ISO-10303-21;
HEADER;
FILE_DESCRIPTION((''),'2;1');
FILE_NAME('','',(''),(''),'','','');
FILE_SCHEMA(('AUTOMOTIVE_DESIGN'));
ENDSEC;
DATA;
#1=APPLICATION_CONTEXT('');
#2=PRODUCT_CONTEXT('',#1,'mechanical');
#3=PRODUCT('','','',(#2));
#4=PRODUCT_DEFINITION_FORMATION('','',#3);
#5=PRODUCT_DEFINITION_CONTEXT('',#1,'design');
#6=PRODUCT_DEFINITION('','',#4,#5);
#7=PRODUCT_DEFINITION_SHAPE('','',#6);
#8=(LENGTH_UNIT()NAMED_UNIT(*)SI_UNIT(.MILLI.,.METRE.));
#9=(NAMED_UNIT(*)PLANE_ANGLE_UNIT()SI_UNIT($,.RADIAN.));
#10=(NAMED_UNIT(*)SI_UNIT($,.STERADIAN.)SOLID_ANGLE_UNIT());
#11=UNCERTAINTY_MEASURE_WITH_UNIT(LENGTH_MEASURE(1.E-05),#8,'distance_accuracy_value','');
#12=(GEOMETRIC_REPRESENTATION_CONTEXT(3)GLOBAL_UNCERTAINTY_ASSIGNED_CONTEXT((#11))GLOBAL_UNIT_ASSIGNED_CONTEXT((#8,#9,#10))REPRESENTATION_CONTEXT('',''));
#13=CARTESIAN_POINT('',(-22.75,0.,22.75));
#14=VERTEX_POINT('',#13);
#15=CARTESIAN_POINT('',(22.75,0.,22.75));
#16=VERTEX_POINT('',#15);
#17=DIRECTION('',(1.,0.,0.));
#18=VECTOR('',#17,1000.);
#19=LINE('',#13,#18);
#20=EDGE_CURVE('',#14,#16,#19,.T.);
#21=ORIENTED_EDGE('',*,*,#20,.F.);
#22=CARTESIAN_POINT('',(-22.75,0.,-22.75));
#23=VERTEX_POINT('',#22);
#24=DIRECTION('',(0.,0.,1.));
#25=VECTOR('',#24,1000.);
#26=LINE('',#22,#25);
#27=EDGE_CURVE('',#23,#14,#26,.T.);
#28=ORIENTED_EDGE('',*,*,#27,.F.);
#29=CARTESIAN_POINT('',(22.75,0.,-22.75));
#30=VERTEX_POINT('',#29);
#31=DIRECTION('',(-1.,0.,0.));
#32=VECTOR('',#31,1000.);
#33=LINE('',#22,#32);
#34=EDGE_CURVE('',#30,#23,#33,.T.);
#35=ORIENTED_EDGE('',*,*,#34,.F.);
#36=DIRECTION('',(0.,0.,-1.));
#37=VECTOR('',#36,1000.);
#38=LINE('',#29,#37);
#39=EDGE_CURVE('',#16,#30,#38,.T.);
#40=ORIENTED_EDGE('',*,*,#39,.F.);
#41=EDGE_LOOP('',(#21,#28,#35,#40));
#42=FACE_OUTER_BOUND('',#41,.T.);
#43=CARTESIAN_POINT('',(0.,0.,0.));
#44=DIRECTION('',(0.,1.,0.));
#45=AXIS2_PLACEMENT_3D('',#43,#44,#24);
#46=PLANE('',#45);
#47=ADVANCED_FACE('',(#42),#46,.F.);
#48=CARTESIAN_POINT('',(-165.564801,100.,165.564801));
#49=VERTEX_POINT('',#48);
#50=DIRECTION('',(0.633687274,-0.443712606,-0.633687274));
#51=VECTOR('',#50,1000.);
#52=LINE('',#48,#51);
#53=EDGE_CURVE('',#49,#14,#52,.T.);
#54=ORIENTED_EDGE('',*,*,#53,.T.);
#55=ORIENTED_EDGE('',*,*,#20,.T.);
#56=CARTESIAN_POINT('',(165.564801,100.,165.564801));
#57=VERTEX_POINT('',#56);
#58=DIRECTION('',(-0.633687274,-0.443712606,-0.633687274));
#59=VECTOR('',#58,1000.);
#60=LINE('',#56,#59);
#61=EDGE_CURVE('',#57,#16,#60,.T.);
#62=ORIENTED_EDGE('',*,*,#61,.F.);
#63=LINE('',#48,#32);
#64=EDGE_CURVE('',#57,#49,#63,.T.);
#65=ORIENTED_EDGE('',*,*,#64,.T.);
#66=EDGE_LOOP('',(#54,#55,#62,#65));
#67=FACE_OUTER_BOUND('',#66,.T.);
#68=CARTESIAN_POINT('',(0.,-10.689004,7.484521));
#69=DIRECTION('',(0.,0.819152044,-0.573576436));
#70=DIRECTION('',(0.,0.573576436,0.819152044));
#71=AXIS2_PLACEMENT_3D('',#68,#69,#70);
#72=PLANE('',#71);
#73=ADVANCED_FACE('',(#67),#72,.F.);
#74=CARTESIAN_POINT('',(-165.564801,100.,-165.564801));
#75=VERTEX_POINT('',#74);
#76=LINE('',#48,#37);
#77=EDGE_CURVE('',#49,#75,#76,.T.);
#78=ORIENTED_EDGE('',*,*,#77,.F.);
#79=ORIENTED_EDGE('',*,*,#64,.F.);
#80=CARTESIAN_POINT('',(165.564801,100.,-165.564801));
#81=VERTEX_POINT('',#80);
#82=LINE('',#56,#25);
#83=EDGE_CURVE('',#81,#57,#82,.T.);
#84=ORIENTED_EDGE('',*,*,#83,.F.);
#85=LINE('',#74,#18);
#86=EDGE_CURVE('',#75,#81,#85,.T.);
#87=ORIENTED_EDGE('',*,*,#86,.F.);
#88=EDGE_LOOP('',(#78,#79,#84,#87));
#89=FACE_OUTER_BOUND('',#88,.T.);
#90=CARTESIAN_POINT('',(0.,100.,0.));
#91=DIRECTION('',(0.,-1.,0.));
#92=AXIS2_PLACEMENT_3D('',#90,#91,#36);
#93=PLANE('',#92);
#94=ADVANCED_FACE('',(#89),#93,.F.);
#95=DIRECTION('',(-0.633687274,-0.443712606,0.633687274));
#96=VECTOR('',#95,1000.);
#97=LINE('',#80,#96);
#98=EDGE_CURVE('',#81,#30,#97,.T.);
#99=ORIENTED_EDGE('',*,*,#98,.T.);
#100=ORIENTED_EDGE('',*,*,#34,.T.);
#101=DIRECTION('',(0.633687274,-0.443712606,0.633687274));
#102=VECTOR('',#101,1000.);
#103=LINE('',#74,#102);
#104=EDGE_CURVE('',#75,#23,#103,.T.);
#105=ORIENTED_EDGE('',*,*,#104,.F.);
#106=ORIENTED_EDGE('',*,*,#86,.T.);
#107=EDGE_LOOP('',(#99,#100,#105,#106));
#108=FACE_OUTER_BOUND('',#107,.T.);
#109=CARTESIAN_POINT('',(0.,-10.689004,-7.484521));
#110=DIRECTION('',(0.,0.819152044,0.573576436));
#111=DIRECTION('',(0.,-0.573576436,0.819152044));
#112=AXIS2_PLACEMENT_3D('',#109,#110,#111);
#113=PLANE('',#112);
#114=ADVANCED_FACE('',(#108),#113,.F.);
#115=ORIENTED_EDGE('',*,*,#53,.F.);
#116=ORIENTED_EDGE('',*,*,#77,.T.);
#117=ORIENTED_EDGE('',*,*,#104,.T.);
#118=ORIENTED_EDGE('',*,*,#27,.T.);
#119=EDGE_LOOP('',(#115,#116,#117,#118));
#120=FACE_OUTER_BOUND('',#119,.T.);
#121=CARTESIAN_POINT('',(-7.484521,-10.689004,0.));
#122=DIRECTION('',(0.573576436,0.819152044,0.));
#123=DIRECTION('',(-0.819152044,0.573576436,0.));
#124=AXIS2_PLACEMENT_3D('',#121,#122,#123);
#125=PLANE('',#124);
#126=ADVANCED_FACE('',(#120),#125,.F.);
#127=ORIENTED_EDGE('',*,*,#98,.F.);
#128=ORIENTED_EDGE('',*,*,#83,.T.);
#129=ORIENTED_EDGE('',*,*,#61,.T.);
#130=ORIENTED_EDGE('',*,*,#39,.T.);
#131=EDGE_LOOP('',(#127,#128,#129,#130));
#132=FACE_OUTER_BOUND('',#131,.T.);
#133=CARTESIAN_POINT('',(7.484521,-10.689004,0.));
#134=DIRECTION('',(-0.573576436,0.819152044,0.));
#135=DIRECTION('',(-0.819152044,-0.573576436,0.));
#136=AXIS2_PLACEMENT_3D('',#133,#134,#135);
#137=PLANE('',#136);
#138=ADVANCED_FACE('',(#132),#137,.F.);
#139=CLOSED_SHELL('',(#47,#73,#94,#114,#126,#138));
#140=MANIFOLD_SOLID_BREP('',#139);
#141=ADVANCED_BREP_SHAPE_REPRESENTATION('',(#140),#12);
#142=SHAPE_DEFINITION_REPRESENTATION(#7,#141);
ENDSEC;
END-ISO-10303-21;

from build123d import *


with BuildPart() as part:
    # 草图5 → 放样1 section 0
    with BuildSketch(Plane(origin=(0, 100, 0), x_dir=(-1, 0, 0), z_dir=(0, -1, 0))):
        with BuildLine():
            Line((165.564800674, -165.564800674), (-165.564800674, -165.564800674))
            Line((-165.564800674, -165.564800674), (-165.564800674, 165.564800674))
            Line((-165.564800674, 165.564800674), (165.564800674, 165.564800674))
            Line((165.564800674, 165.564800674), (165.564800674, -165.564800674))
        make_face()
    # 草图1 → 放样1 section 1
    with BuildSketch(Plane(origin=(0, 0, 0), x_dir=(1, 0, 0), z_dir=(0, 1, 0))):
        with BuildLine():
            Line((-22.75, 22.75), (22.75, 22.75))
            Line((22.75, 22.75), (22.75, -22.75))
            Line((22.75, -22.75), (-22.75, -22.75))
            Line((-22.75, -22.75), (-22.75, 22.75))
        make_face()
    loft()


solid = part.part
